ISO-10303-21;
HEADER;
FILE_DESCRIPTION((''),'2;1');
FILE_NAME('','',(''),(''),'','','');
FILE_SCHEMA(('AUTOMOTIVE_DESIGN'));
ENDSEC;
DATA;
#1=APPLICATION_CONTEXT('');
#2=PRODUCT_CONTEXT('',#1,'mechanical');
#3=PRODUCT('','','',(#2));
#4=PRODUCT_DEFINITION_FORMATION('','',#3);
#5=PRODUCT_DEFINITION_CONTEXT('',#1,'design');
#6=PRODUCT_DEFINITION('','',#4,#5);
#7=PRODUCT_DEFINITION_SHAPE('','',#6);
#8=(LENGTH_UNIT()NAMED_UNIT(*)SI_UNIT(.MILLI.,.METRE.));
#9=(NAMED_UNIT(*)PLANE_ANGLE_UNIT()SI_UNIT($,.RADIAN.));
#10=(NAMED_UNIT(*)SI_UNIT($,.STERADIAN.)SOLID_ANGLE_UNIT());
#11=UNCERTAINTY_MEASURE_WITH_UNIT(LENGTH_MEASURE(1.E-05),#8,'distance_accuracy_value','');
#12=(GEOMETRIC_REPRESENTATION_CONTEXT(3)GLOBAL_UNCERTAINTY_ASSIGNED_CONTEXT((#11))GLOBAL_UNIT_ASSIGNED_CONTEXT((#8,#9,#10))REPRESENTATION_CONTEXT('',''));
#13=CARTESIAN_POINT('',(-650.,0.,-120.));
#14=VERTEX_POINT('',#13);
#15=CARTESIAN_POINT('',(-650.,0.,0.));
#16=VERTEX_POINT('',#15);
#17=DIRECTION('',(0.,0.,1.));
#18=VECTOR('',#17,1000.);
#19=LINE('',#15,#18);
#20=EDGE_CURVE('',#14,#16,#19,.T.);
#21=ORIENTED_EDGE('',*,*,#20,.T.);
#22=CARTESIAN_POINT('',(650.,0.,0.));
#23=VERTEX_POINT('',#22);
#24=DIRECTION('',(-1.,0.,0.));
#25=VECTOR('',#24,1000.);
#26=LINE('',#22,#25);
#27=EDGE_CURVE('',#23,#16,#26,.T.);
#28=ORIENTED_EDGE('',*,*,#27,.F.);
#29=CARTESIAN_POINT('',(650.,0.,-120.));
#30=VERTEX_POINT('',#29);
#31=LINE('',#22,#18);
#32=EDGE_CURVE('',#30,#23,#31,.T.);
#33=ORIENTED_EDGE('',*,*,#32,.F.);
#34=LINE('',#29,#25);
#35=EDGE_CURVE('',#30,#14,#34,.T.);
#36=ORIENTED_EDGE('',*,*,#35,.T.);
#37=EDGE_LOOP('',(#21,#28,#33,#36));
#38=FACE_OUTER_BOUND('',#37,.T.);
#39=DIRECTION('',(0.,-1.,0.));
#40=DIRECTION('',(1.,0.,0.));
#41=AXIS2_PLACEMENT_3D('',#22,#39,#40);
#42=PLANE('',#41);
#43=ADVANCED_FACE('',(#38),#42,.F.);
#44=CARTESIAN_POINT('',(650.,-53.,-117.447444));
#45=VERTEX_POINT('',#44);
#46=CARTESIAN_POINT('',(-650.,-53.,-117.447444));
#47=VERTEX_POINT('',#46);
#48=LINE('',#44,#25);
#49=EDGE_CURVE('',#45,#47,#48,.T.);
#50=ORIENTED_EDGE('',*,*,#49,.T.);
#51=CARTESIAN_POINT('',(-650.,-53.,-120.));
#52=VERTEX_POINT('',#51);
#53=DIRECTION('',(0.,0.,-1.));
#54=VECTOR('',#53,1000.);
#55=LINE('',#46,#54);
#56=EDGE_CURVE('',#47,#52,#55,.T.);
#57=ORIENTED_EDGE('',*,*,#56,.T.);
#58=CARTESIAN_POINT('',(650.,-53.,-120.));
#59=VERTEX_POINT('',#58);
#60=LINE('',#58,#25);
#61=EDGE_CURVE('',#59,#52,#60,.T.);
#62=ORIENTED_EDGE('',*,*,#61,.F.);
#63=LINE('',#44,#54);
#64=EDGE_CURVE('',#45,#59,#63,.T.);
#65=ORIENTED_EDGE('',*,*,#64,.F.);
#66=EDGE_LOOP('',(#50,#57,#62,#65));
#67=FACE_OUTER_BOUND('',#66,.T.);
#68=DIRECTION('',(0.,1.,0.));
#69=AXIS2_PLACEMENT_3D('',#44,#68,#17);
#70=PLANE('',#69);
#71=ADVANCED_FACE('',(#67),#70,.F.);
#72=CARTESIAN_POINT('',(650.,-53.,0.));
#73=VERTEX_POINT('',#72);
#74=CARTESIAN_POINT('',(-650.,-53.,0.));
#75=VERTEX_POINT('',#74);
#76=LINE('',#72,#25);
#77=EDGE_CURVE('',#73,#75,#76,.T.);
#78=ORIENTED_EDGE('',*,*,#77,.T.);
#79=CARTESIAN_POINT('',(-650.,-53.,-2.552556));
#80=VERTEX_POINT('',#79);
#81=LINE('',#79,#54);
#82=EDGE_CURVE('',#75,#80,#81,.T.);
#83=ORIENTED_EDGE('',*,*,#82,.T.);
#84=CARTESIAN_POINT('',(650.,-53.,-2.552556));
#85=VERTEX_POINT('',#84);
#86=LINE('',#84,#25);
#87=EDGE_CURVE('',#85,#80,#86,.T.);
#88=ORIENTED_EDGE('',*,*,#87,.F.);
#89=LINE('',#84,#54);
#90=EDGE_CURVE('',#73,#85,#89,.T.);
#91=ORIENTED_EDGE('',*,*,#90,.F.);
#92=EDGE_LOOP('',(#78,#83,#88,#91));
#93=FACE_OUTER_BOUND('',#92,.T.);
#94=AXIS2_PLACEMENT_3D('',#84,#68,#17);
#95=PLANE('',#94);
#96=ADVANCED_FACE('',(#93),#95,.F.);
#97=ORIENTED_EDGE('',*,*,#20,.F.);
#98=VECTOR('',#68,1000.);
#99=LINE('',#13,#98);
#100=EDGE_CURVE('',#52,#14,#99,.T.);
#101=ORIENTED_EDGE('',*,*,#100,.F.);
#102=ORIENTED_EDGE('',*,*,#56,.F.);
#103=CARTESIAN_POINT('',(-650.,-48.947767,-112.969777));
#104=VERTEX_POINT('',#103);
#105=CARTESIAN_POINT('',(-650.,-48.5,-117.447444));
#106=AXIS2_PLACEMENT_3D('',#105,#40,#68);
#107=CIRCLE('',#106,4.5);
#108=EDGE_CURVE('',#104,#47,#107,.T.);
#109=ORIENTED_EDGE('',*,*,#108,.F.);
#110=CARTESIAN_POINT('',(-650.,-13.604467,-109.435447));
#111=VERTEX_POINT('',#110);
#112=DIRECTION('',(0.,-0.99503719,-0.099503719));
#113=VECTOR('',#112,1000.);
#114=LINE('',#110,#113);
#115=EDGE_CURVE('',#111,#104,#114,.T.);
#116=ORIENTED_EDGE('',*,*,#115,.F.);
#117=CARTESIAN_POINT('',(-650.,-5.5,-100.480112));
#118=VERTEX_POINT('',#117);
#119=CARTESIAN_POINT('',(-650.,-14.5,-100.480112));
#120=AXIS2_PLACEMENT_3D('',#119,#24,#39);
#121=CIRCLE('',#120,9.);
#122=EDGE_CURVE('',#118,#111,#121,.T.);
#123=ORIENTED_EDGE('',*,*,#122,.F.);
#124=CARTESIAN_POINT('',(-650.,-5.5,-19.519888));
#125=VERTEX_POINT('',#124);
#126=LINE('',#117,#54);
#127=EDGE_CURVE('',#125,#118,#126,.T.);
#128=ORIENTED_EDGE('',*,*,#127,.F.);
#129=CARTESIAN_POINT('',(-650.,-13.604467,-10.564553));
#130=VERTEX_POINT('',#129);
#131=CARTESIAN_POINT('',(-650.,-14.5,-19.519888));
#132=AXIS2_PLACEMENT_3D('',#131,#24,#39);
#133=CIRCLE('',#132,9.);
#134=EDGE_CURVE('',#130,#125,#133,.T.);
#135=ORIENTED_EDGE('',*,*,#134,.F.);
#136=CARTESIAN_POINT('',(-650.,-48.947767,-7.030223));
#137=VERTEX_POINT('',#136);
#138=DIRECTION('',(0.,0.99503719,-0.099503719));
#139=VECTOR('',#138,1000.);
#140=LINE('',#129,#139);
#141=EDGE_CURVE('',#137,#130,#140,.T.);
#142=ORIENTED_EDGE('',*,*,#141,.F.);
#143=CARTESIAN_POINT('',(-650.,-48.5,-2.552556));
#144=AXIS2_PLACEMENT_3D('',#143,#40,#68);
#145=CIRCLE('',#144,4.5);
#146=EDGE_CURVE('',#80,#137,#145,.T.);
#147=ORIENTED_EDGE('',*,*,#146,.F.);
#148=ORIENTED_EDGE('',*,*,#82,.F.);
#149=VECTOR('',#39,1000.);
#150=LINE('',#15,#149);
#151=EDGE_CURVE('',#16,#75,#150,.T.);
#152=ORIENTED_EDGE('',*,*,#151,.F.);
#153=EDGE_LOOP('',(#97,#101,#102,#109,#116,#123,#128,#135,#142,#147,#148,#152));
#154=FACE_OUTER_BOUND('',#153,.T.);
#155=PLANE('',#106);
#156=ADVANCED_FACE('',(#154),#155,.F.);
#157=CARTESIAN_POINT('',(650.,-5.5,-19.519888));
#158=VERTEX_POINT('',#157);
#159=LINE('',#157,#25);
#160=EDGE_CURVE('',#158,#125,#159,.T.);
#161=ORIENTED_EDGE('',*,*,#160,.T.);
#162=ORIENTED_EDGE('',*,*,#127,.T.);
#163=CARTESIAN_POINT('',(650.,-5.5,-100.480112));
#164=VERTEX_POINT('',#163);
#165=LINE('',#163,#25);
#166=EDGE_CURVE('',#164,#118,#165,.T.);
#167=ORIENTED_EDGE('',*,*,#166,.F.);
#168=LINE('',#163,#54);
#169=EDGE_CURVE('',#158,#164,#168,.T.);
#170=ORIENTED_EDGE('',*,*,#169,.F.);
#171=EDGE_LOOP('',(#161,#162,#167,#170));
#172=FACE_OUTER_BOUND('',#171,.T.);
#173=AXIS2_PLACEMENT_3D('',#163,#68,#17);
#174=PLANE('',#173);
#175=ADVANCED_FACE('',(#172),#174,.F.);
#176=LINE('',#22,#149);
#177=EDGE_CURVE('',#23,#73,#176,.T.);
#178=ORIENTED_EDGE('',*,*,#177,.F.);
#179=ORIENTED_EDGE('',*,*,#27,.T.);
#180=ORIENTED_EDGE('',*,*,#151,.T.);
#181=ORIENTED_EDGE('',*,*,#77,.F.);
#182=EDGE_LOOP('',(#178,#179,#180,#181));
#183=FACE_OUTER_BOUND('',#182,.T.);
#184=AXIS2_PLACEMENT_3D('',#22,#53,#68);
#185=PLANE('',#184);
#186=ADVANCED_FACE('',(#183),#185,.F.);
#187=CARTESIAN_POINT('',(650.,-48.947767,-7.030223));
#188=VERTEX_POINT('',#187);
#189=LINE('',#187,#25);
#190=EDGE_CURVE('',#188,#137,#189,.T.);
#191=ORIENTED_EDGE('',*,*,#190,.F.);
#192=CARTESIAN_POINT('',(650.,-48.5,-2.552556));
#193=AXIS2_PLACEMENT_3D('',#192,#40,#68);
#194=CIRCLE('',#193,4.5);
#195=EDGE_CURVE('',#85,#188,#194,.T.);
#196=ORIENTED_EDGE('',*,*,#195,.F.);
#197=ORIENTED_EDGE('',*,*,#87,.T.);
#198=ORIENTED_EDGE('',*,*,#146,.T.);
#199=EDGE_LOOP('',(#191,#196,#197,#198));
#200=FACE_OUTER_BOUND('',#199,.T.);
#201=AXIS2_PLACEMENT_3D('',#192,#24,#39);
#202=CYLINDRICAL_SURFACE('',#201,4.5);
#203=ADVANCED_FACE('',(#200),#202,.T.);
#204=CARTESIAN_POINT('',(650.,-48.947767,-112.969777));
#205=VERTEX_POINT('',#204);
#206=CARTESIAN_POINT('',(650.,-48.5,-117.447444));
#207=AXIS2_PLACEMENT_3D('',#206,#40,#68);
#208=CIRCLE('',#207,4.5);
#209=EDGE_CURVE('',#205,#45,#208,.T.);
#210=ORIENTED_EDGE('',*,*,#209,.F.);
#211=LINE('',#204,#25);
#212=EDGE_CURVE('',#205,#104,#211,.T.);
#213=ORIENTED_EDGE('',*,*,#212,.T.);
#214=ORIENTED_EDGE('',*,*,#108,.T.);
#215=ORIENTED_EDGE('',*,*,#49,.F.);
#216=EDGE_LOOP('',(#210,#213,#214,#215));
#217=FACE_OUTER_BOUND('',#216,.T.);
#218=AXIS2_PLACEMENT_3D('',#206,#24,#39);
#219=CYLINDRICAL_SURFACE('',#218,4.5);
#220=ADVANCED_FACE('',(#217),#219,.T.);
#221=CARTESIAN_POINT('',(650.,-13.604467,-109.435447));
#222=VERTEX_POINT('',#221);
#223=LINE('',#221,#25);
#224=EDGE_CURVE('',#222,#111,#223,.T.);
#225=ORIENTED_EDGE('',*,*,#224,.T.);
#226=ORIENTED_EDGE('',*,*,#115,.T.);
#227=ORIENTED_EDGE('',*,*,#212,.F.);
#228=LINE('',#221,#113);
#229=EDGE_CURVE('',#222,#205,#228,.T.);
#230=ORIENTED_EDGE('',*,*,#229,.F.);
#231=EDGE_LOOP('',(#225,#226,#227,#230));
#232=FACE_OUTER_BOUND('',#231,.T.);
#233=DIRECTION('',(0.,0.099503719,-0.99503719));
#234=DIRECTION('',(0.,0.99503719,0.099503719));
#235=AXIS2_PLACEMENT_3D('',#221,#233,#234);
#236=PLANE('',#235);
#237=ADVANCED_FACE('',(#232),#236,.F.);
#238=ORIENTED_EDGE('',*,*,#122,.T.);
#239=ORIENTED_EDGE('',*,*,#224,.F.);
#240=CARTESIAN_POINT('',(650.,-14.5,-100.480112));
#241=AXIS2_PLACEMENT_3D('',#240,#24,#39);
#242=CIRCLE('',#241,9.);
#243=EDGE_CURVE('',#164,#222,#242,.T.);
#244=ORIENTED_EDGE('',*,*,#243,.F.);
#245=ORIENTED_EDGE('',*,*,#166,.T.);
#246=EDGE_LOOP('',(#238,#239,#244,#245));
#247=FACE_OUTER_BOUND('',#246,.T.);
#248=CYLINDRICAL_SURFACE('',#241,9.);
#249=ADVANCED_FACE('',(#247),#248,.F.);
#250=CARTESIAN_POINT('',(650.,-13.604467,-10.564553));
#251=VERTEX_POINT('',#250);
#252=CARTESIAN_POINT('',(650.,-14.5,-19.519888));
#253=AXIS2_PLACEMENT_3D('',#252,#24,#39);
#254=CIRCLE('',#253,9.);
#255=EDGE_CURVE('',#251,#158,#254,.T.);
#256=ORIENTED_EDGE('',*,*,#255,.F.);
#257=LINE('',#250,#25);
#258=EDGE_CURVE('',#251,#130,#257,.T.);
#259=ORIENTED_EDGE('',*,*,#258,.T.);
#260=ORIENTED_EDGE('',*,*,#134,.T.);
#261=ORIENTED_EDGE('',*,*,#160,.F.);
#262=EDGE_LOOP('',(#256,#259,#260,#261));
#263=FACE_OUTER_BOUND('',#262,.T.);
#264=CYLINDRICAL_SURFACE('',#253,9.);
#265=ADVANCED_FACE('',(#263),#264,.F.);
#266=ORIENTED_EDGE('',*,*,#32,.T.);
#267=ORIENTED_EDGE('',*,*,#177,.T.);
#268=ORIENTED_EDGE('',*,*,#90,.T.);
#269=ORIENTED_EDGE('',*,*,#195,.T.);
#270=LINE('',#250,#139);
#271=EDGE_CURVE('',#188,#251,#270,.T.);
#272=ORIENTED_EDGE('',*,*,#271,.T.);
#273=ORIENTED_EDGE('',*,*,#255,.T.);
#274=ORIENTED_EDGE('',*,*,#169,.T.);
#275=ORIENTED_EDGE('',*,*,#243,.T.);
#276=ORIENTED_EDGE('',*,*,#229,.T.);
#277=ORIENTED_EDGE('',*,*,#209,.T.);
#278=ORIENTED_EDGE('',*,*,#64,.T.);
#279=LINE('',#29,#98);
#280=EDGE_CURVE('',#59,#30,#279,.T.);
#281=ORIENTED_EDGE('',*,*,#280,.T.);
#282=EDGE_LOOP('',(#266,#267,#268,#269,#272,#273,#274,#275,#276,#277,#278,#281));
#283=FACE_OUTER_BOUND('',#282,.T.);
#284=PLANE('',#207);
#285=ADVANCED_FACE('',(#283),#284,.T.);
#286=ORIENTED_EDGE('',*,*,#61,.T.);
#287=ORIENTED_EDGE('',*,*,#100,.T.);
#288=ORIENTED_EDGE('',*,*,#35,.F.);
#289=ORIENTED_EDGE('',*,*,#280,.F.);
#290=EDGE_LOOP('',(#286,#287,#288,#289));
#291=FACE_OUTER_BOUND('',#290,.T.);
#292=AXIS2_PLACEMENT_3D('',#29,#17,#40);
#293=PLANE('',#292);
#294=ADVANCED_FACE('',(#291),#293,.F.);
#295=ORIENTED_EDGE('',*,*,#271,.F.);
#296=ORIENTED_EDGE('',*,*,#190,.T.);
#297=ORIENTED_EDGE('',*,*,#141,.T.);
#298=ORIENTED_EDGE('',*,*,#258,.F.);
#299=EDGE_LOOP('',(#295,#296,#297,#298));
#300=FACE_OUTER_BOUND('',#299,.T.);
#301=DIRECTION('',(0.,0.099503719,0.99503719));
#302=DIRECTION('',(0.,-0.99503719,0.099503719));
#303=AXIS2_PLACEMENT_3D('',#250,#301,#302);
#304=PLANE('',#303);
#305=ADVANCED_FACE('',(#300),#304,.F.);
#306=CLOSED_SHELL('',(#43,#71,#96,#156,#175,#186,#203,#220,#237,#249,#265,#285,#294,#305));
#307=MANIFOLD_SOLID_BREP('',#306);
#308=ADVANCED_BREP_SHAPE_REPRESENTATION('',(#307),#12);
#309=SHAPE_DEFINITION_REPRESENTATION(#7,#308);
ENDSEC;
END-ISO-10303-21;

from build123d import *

# Parameters (mm, degrees)
STRUCTURAL_MEMBER1_DEPTH = 1300


with BuildPart() as part:
    # Sketch1 → Structural Member1 (new body)
    with BuildSketch(Plane.YZ.offset(-650)):
        with BuildLine():
            Line((0, 0), (0, -120))
            Line((0, -120), (-53, -120))
            Line((-53, -120), (-53, -117.44744403))
            ThreePointArc((-53, -117.44744403), (-51.836536401, -114.427920086), (-48.947766736, -112.969776674))
            Line((-48.947766736, -112.969776674), (-13.604466529, -109.435446653))
            ThreePointArc((-13.604466529, -109.435446653), (-7.826927198, -106.519159828), (-5.5, -100.480111941))
            Line((-5.5, -100.480111941), (-5.5, -19.519888059))
            ThreePointArc((-5.5, -19.519888059), (-7.826927198, -13.480840172), (-13.604466529, -10.564553347))
            Line((-13.604466529, -10.564553347), (-48.947766736, -7.030223326))
            ThreePointArc((-48.947766736, -7.030223326), (-51.836536401, -5.572079914), (-53, -2.55255597))
            Line((-53, -2.55255597), (-53, 0))
            Line((-53, 0), (0, 0))
        make_face()
    extrude(amount=STRUCTURAL_MEMBER1_DEPTH)


solid = part.part
